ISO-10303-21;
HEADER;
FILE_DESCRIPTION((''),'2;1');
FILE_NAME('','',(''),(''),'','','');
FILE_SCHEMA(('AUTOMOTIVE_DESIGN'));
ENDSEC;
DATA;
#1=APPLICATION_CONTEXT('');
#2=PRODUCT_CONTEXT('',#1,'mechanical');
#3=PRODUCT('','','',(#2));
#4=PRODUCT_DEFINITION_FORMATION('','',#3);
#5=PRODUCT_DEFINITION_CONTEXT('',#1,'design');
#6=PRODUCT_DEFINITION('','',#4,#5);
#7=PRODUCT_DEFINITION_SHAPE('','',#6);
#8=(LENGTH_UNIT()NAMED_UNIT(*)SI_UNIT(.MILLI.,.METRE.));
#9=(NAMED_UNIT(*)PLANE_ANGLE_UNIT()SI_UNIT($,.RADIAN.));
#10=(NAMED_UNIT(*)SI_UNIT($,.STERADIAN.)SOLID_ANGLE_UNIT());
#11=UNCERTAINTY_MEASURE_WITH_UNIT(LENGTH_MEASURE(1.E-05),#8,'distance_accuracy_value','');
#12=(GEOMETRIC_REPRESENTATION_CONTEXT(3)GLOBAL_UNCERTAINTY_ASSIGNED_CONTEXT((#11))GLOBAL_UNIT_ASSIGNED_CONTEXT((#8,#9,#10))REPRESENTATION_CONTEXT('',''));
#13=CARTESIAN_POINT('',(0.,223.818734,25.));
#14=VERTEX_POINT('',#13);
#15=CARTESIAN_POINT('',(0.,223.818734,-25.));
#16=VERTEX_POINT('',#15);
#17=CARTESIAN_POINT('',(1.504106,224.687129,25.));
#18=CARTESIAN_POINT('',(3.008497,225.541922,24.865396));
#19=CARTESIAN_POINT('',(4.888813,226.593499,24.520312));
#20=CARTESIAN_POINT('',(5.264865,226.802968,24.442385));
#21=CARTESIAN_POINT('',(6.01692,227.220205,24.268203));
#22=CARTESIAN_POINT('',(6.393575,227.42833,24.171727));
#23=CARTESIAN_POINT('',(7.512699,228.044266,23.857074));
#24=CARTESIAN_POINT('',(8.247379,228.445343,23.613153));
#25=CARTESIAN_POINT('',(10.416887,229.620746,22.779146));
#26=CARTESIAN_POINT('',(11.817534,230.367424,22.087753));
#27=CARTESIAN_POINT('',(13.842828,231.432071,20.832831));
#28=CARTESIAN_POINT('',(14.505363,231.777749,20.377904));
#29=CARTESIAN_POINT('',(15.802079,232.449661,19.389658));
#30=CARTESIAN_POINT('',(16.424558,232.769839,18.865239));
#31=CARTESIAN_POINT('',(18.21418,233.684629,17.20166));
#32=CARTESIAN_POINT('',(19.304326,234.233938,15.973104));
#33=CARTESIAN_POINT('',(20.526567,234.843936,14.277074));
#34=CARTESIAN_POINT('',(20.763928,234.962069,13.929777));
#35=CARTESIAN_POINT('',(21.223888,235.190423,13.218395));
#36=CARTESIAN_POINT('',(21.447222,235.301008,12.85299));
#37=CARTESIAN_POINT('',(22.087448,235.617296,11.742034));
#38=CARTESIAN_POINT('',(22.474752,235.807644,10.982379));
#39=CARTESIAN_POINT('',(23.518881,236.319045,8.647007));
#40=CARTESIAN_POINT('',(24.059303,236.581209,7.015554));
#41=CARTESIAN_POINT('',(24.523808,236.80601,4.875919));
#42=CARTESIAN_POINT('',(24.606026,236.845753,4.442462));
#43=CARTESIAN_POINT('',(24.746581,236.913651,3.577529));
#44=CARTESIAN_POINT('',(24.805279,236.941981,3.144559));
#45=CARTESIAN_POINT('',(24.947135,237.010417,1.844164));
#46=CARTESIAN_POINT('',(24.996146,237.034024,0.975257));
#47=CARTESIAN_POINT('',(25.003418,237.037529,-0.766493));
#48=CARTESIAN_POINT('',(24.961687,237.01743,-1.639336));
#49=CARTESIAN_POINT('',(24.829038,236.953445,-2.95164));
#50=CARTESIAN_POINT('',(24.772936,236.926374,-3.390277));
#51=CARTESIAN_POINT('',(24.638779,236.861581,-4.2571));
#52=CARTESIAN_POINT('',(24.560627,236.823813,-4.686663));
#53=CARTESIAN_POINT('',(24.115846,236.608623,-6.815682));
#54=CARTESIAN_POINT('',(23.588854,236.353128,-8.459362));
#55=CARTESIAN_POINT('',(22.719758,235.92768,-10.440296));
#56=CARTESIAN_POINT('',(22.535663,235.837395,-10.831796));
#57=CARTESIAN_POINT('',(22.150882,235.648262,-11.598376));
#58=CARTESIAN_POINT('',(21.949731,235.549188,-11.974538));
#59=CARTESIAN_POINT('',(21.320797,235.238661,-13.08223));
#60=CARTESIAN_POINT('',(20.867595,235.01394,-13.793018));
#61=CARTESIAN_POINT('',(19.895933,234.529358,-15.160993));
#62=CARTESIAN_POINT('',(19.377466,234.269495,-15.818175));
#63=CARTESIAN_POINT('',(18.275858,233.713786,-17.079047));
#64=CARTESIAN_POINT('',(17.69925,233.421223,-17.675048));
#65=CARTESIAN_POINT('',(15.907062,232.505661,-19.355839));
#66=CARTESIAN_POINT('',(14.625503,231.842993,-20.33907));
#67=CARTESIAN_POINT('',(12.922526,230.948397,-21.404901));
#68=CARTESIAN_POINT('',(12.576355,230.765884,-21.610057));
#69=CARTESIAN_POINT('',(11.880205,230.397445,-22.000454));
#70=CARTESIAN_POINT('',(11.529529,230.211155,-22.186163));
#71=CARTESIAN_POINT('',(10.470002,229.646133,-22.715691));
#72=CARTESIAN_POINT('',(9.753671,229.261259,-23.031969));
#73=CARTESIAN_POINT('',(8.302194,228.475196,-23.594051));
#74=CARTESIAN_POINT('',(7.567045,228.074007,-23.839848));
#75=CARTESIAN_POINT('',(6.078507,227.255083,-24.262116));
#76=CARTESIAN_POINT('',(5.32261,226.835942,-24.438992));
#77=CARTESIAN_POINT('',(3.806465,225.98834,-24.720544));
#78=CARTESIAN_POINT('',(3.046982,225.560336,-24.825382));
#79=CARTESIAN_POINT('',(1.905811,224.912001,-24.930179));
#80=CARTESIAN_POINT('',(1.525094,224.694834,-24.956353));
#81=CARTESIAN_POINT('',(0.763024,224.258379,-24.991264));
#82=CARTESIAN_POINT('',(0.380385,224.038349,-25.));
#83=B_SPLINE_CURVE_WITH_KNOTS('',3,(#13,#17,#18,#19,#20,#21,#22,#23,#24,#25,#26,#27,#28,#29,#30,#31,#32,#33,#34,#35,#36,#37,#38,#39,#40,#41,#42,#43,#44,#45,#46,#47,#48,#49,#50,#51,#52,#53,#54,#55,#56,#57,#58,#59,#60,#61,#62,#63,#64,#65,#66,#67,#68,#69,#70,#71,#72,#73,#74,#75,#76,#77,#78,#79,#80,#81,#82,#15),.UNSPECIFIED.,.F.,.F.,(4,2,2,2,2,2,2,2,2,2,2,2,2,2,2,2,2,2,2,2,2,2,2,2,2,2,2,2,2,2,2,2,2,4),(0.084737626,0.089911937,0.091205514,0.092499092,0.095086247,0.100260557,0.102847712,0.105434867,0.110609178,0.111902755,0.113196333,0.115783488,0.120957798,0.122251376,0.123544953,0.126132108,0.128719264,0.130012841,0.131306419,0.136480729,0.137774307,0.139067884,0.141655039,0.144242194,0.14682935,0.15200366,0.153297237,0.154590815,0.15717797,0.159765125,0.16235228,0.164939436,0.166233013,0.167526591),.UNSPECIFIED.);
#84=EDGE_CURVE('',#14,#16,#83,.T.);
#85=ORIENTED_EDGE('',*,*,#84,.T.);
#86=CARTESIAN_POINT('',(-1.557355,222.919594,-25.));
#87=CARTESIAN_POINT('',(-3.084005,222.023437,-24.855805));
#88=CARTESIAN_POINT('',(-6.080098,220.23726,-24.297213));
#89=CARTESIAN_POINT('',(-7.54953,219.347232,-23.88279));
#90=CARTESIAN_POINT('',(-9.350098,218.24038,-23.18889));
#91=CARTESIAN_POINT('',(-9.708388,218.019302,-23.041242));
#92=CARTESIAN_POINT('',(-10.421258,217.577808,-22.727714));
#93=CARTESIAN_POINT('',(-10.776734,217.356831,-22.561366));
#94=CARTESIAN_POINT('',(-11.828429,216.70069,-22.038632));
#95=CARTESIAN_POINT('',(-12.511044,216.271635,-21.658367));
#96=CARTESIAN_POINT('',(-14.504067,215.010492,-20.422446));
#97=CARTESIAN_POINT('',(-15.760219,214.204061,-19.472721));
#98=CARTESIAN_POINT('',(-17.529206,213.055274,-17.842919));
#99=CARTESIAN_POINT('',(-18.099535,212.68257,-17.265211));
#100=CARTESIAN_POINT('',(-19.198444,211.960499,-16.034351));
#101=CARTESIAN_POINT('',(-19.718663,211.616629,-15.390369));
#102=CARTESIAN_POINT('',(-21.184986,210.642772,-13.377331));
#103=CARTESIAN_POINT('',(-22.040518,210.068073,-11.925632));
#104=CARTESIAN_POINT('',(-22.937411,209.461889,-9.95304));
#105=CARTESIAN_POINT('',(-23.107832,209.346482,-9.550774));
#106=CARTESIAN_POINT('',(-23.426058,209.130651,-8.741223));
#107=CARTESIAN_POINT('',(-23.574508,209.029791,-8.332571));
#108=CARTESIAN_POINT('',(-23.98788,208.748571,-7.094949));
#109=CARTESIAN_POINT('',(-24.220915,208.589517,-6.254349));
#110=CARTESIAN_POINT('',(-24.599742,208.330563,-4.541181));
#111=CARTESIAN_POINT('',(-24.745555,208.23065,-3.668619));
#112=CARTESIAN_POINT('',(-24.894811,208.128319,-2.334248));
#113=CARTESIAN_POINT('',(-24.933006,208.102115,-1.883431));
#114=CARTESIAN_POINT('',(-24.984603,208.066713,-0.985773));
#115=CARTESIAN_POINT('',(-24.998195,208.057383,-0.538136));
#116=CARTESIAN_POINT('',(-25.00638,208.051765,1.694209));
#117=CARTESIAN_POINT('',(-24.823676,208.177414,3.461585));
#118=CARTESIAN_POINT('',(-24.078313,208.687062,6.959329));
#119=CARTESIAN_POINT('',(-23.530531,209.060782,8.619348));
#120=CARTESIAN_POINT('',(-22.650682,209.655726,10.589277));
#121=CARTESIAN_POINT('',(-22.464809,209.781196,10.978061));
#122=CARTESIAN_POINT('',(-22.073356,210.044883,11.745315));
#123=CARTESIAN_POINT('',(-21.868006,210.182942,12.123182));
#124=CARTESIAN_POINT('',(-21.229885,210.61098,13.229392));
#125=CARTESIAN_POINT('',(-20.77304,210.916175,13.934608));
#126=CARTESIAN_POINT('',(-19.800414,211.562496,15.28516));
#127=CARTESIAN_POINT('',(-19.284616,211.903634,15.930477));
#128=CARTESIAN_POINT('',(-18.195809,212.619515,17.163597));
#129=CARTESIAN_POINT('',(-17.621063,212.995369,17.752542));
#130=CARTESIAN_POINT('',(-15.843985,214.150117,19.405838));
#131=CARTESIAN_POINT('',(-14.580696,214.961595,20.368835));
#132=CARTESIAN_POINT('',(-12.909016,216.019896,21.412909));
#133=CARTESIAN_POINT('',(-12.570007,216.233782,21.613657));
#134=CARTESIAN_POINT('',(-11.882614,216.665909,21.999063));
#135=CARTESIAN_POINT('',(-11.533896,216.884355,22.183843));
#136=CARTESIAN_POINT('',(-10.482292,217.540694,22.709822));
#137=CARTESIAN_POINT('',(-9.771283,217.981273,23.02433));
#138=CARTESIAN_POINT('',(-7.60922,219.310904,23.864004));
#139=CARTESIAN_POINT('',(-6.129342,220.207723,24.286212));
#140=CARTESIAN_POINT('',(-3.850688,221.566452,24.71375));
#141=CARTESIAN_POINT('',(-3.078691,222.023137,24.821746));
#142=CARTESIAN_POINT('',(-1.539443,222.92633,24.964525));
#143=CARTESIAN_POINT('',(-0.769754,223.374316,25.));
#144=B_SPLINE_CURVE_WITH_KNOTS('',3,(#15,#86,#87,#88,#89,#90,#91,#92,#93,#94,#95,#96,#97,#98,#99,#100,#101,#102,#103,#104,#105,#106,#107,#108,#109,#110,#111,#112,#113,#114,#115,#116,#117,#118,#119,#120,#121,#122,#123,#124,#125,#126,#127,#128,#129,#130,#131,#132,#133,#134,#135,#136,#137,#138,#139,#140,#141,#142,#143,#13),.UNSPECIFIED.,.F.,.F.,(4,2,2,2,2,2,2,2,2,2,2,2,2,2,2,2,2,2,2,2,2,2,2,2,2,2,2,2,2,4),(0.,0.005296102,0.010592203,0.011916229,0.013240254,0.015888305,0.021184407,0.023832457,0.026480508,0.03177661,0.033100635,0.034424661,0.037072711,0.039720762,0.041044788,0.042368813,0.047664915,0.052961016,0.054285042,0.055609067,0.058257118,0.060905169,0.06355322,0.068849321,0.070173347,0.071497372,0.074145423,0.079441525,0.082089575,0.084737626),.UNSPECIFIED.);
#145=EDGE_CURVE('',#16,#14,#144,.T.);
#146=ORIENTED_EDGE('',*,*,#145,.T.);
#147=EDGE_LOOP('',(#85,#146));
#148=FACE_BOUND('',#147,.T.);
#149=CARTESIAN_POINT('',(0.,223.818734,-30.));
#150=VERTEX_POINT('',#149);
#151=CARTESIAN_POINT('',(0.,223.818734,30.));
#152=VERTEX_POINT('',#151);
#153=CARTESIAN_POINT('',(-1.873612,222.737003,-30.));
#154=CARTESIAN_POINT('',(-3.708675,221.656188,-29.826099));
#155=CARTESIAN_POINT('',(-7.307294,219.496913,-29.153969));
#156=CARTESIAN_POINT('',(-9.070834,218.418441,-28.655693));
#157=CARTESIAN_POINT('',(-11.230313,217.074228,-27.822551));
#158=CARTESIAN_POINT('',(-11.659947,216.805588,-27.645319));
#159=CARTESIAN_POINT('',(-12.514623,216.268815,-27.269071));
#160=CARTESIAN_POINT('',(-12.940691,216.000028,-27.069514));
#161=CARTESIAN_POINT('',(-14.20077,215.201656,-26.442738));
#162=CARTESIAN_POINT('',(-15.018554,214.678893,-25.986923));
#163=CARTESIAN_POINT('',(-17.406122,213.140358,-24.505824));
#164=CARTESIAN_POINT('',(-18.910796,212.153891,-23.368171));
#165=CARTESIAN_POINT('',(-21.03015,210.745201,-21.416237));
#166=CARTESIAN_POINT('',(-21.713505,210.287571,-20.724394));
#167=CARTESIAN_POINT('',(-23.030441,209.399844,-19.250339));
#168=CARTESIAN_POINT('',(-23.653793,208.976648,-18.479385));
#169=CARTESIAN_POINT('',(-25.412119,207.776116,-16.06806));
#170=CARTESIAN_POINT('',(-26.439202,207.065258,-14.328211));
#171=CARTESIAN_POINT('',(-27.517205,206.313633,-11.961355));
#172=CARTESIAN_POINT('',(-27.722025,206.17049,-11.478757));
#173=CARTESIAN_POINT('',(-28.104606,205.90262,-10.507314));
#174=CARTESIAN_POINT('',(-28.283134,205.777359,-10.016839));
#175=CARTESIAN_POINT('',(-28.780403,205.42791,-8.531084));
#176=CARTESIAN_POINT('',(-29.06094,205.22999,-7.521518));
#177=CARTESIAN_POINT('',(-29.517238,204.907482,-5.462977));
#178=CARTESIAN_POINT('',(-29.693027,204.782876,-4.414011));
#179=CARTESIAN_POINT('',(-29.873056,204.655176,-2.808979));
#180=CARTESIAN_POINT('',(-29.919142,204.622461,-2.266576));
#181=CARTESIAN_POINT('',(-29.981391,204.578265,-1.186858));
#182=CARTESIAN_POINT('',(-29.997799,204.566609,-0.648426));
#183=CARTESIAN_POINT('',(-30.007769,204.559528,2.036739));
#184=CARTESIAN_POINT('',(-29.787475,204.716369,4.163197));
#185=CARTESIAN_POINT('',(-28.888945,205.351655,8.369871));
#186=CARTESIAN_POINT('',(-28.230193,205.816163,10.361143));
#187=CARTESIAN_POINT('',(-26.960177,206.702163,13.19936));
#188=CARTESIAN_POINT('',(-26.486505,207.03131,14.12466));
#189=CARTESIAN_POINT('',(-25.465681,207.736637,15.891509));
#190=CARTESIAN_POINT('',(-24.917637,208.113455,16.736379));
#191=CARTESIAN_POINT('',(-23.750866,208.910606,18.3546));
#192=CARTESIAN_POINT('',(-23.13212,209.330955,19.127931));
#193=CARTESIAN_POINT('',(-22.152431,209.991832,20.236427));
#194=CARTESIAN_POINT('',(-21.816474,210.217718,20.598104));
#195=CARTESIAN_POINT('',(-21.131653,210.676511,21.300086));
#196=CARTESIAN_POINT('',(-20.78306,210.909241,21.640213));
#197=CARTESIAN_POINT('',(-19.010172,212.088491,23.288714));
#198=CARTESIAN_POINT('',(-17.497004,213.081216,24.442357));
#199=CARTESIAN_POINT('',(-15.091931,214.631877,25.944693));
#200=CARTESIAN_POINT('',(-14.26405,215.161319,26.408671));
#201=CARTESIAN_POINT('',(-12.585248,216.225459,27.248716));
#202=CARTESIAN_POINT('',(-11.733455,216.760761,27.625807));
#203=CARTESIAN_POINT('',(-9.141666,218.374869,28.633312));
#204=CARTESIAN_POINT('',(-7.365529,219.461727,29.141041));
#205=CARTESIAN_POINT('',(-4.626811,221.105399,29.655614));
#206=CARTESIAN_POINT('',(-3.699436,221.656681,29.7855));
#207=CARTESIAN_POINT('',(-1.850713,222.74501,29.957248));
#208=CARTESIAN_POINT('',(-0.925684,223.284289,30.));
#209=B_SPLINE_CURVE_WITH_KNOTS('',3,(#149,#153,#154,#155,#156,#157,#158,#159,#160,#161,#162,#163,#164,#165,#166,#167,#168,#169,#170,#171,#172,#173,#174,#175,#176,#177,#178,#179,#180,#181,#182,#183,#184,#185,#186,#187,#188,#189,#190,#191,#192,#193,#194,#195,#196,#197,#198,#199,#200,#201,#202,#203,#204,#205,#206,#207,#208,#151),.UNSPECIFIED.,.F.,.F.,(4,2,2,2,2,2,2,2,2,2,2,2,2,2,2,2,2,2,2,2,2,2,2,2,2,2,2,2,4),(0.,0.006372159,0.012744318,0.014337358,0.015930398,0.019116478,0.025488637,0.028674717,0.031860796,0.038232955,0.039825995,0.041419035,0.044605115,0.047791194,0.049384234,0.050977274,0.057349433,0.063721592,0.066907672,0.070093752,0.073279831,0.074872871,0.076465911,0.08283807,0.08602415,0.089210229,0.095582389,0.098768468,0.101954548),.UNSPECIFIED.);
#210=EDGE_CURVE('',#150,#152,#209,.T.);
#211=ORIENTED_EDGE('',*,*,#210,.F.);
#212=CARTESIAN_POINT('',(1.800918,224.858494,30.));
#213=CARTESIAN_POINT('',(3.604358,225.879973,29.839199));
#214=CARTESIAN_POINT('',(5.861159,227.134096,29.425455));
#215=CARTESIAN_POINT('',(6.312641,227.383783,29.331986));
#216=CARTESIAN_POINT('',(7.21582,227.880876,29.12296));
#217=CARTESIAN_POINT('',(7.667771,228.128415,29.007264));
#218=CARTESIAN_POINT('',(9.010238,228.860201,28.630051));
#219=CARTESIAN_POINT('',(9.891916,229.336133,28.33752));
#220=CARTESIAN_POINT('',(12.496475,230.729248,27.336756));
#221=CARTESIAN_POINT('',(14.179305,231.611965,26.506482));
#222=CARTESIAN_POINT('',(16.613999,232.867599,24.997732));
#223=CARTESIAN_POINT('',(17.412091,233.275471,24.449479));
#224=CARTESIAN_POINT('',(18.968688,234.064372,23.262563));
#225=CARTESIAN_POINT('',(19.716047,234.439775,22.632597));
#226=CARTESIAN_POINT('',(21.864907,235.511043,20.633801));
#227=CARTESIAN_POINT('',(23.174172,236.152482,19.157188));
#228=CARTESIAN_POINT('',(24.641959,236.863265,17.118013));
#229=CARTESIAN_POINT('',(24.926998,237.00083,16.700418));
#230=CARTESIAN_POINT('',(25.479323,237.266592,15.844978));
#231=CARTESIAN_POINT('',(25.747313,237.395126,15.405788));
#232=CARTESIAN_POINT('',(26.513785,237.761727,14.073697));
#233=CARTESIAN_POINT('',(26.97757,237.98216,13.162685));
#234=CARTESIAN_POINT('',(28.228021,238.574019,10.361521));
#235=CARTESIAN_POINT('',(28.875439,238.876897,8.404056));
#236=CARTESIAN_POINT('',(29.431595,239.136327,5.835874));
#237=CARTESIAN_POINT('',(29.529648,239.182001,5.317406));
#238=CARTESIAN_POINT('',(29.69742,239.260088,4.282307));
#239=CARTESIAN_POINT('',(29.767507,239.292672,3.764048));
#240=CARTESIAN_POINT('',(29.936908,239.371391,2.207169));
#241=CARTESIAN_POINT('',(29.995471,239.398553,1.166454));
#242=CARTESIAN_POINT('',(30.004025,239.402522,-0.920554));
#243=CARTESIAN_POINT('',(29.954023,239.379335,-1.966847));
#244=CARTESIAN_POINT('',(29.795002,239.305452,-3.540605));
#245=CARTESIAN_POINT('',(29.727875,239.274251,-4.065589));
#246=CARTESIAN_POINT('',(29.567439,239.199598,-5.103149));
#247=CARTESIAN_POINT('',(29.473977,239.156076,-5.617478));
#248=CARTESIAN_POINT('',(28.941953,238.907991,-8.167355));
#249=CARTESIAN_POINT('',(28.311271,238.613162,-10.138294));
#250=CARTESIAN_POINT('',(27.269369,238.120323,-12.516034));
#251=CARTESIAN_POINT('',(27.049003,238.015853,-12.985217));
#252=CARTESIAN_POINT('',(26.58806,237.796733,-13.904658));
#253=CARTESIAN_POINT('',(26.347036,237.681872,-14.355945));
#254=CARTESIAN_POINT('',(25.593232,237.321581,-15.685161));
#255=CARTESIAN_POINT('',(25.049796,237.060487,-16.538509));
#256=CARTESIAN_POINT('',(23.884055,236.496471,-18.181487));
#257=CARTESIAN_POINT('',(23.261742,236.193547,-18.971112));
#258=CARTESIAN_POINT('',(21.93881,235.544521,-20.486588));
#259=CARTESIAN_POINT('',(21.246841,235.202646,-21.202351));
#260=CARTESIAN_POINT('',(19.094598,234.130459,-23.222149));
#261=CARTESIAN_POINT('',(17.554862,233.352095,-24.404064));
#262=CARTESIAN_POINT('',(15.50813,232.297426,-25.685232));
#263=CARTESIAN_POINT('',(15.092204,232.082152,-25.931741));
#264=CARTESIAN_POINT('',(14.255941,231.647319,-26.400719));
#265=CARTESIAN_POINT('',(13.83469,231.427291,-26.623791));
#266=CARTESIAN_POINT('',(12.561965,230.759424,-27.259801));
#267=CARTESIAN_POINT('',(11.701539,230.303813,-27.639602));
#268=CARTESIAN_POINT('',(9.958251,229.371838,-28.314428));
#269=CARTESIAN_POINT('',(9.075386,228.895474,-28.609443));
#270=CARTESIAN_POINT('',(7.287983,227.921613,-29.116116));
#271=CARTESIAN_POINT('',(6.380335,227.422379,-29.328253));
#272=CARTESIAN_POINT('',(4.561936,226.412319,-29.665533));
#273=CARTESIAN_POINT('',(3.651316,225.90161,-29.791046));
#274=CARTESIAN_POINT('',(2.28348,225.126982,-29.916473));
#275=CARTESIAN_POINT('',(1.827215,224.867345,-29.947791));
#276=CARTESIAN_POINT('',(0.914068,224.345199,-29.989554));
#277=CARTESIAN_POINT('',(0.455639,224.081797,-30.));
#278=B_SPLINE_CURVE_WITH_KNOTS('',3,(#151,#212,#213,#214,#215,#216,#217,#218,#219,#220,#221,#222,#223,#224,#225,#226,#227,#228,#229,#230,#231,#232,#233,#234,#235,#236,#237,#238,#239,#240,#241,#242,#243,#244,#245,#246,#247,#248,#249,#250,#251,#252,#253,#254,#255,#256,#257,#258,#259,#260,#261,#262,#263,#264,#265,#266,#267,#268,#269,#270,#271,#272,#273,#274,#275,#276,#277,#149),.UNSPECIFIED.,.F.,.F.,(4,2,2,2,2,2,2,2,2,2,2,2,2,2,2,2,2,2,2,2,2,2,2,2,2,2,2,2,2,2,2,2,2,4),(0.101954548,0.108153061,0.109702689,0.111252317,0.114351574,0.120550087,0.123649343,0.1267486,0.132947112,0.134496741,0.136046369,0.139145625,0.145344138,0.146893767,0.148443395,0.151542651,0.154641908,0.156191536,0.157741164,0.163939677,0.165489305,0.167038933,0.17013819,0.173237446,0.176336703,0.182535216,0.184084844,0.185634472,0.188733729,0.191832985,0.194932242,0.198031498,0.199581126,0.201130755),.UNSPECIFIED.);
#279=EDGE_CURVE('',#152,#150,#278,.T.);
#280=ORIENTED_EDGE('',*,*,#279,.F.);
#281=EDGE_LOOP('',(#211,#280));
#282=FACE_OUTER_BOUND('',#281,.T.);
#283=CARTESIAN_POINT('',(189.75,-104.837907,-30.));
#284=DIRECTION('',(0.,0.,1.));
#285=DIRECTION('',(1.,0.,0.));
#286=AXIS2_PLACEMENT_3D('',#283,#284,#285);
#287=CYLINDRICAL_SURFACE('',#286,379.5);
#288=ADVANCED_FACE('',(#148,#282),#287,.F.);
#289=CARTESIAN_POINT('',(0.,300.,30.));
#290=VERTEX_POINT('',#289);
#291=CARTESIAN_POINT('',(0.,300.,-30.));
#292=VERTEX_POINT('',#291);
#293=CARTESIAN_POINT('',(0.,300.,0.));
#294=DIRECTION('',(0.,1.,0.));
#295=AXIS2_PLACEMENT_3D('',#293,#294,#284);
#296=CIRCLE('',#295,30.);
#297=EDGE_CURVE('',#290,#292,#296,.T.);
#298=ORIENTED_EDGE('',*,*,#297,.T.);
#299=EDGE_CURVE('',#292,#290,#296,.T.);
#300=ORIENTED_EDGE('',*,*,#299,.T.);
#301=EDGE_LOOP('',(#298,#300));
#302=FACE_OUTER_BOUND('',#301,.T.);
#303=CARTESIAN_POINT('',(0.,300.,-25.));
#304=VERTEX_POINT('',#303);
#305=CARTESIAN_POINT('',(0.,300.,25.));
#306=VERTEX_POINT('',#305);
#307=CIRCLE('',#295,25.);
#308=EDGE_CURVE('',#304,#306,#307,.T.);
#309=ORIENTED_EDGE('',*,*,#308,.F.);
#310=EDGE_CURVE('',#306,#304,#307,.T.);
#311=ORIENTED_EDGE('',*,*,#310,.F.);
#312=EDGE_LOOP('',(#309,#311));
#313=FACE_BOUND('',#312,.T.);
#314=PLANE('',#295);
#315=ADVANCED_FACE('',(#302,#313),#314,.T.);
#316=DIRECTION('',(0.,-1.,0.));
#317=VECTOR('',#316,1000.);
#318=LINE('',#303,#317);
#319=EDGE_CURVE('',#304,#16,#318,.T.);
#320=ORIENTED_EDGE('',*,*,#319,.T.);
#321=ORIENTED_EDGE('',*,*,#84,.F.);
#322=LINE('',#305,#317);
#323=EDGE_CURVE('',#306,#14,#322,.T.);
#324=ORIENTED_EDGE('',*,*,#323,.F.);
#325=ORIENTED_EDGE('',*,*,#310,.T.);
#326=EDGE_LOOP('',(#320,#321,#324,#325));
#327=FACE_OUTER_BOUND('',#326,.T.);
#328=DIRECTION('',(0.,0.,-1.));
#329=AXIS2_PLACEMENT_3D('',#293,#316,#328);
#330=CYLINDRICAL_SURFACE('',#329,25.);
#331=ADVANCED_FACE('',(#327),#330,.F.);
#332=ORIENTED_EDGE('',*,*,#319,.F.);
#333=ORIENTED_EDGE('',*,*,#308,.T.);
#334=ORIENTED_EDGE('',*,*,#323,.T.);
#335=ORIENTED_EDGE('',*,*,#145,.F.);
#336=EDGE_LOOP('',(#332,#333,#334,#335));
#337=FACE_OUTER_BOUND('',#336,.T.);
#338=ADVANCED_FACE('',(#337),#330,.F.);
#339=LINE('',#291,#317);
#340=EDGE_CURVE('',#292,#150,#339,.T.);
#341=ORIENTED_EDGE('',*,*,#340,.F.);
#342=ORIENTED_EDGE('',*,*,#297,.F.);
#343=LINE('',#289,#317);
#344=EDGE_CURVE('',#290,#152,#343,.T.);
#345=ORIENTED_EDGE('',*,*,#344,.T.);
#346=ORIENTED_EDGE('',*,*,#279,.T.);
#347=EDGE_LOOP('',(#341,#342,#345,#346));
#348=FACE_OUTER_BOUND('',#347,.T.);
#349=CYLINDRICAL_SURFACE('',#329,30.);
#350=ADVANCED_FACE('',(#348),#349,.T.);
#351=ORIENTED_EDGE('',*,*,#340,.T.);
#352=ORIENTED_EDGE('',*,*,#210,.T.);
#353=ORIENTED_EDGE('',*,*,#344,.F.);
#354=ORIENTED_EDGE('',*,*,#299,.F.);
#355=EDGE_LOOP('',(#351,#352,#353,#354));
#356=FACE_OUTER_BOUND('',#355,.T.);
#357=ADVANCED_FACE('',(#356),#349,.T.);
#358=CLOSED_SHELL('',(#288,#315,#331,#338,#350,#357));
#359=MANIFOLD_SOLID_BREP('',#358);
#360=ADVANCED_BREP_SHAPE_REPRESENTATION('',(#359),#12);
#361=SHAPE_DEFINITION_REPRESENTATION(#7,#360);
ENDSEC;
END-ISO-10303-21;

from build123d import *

# Parameters (mm, degrees)
SKETCH2_R               = 30
SKETCH2_R_2             = 25
BOSS_EXTRUDE1_DEPTH     = 300
CUT_EXTRUDE1_DEPTH      = 303.985148151
CUT_EXTRUDE1_DEPTH_BACK = 303.985148151
SKETCH3_R               = 379.5


with BuildPart() as part:
    # Sketch2 → Boss-Extrude1 (new body)
    with BuildSketch(Plane(origin=(0, 0, 0), x_dir=(1, 0, 0), z_dir=(0, 1, 0))):
        with Locations(Location((0, 0, 0), (0, 0, 270))):
            Circle(SKETCH2_R)
        with Locations(Location((0, 0, 0), (0, 0, 270))):
            Circle(SKETCH2_R_2, mode=Mode.SUBTRACT)
    extrude(amount=BOSS_EXTRUDE1_DEPTH)

    # Sketch3 → Cut-Extrude1 (cut, two sides: drawn at the far end of the back side and taken through both)
    with BuildSketch(Plane.XY.offset(-CUT_EXTRUDE1_DEPTH_BACK)):
        with Locations((189.75, -104.83790721)):
            Circle(SKETCH3_R)
    extrude(amount=CUT_EXTRUDE1_DEPTH + CUT_EXTRUDE1_DEPTH_BACK, mode=Mode.SUBTRACT)


solid = part.part
